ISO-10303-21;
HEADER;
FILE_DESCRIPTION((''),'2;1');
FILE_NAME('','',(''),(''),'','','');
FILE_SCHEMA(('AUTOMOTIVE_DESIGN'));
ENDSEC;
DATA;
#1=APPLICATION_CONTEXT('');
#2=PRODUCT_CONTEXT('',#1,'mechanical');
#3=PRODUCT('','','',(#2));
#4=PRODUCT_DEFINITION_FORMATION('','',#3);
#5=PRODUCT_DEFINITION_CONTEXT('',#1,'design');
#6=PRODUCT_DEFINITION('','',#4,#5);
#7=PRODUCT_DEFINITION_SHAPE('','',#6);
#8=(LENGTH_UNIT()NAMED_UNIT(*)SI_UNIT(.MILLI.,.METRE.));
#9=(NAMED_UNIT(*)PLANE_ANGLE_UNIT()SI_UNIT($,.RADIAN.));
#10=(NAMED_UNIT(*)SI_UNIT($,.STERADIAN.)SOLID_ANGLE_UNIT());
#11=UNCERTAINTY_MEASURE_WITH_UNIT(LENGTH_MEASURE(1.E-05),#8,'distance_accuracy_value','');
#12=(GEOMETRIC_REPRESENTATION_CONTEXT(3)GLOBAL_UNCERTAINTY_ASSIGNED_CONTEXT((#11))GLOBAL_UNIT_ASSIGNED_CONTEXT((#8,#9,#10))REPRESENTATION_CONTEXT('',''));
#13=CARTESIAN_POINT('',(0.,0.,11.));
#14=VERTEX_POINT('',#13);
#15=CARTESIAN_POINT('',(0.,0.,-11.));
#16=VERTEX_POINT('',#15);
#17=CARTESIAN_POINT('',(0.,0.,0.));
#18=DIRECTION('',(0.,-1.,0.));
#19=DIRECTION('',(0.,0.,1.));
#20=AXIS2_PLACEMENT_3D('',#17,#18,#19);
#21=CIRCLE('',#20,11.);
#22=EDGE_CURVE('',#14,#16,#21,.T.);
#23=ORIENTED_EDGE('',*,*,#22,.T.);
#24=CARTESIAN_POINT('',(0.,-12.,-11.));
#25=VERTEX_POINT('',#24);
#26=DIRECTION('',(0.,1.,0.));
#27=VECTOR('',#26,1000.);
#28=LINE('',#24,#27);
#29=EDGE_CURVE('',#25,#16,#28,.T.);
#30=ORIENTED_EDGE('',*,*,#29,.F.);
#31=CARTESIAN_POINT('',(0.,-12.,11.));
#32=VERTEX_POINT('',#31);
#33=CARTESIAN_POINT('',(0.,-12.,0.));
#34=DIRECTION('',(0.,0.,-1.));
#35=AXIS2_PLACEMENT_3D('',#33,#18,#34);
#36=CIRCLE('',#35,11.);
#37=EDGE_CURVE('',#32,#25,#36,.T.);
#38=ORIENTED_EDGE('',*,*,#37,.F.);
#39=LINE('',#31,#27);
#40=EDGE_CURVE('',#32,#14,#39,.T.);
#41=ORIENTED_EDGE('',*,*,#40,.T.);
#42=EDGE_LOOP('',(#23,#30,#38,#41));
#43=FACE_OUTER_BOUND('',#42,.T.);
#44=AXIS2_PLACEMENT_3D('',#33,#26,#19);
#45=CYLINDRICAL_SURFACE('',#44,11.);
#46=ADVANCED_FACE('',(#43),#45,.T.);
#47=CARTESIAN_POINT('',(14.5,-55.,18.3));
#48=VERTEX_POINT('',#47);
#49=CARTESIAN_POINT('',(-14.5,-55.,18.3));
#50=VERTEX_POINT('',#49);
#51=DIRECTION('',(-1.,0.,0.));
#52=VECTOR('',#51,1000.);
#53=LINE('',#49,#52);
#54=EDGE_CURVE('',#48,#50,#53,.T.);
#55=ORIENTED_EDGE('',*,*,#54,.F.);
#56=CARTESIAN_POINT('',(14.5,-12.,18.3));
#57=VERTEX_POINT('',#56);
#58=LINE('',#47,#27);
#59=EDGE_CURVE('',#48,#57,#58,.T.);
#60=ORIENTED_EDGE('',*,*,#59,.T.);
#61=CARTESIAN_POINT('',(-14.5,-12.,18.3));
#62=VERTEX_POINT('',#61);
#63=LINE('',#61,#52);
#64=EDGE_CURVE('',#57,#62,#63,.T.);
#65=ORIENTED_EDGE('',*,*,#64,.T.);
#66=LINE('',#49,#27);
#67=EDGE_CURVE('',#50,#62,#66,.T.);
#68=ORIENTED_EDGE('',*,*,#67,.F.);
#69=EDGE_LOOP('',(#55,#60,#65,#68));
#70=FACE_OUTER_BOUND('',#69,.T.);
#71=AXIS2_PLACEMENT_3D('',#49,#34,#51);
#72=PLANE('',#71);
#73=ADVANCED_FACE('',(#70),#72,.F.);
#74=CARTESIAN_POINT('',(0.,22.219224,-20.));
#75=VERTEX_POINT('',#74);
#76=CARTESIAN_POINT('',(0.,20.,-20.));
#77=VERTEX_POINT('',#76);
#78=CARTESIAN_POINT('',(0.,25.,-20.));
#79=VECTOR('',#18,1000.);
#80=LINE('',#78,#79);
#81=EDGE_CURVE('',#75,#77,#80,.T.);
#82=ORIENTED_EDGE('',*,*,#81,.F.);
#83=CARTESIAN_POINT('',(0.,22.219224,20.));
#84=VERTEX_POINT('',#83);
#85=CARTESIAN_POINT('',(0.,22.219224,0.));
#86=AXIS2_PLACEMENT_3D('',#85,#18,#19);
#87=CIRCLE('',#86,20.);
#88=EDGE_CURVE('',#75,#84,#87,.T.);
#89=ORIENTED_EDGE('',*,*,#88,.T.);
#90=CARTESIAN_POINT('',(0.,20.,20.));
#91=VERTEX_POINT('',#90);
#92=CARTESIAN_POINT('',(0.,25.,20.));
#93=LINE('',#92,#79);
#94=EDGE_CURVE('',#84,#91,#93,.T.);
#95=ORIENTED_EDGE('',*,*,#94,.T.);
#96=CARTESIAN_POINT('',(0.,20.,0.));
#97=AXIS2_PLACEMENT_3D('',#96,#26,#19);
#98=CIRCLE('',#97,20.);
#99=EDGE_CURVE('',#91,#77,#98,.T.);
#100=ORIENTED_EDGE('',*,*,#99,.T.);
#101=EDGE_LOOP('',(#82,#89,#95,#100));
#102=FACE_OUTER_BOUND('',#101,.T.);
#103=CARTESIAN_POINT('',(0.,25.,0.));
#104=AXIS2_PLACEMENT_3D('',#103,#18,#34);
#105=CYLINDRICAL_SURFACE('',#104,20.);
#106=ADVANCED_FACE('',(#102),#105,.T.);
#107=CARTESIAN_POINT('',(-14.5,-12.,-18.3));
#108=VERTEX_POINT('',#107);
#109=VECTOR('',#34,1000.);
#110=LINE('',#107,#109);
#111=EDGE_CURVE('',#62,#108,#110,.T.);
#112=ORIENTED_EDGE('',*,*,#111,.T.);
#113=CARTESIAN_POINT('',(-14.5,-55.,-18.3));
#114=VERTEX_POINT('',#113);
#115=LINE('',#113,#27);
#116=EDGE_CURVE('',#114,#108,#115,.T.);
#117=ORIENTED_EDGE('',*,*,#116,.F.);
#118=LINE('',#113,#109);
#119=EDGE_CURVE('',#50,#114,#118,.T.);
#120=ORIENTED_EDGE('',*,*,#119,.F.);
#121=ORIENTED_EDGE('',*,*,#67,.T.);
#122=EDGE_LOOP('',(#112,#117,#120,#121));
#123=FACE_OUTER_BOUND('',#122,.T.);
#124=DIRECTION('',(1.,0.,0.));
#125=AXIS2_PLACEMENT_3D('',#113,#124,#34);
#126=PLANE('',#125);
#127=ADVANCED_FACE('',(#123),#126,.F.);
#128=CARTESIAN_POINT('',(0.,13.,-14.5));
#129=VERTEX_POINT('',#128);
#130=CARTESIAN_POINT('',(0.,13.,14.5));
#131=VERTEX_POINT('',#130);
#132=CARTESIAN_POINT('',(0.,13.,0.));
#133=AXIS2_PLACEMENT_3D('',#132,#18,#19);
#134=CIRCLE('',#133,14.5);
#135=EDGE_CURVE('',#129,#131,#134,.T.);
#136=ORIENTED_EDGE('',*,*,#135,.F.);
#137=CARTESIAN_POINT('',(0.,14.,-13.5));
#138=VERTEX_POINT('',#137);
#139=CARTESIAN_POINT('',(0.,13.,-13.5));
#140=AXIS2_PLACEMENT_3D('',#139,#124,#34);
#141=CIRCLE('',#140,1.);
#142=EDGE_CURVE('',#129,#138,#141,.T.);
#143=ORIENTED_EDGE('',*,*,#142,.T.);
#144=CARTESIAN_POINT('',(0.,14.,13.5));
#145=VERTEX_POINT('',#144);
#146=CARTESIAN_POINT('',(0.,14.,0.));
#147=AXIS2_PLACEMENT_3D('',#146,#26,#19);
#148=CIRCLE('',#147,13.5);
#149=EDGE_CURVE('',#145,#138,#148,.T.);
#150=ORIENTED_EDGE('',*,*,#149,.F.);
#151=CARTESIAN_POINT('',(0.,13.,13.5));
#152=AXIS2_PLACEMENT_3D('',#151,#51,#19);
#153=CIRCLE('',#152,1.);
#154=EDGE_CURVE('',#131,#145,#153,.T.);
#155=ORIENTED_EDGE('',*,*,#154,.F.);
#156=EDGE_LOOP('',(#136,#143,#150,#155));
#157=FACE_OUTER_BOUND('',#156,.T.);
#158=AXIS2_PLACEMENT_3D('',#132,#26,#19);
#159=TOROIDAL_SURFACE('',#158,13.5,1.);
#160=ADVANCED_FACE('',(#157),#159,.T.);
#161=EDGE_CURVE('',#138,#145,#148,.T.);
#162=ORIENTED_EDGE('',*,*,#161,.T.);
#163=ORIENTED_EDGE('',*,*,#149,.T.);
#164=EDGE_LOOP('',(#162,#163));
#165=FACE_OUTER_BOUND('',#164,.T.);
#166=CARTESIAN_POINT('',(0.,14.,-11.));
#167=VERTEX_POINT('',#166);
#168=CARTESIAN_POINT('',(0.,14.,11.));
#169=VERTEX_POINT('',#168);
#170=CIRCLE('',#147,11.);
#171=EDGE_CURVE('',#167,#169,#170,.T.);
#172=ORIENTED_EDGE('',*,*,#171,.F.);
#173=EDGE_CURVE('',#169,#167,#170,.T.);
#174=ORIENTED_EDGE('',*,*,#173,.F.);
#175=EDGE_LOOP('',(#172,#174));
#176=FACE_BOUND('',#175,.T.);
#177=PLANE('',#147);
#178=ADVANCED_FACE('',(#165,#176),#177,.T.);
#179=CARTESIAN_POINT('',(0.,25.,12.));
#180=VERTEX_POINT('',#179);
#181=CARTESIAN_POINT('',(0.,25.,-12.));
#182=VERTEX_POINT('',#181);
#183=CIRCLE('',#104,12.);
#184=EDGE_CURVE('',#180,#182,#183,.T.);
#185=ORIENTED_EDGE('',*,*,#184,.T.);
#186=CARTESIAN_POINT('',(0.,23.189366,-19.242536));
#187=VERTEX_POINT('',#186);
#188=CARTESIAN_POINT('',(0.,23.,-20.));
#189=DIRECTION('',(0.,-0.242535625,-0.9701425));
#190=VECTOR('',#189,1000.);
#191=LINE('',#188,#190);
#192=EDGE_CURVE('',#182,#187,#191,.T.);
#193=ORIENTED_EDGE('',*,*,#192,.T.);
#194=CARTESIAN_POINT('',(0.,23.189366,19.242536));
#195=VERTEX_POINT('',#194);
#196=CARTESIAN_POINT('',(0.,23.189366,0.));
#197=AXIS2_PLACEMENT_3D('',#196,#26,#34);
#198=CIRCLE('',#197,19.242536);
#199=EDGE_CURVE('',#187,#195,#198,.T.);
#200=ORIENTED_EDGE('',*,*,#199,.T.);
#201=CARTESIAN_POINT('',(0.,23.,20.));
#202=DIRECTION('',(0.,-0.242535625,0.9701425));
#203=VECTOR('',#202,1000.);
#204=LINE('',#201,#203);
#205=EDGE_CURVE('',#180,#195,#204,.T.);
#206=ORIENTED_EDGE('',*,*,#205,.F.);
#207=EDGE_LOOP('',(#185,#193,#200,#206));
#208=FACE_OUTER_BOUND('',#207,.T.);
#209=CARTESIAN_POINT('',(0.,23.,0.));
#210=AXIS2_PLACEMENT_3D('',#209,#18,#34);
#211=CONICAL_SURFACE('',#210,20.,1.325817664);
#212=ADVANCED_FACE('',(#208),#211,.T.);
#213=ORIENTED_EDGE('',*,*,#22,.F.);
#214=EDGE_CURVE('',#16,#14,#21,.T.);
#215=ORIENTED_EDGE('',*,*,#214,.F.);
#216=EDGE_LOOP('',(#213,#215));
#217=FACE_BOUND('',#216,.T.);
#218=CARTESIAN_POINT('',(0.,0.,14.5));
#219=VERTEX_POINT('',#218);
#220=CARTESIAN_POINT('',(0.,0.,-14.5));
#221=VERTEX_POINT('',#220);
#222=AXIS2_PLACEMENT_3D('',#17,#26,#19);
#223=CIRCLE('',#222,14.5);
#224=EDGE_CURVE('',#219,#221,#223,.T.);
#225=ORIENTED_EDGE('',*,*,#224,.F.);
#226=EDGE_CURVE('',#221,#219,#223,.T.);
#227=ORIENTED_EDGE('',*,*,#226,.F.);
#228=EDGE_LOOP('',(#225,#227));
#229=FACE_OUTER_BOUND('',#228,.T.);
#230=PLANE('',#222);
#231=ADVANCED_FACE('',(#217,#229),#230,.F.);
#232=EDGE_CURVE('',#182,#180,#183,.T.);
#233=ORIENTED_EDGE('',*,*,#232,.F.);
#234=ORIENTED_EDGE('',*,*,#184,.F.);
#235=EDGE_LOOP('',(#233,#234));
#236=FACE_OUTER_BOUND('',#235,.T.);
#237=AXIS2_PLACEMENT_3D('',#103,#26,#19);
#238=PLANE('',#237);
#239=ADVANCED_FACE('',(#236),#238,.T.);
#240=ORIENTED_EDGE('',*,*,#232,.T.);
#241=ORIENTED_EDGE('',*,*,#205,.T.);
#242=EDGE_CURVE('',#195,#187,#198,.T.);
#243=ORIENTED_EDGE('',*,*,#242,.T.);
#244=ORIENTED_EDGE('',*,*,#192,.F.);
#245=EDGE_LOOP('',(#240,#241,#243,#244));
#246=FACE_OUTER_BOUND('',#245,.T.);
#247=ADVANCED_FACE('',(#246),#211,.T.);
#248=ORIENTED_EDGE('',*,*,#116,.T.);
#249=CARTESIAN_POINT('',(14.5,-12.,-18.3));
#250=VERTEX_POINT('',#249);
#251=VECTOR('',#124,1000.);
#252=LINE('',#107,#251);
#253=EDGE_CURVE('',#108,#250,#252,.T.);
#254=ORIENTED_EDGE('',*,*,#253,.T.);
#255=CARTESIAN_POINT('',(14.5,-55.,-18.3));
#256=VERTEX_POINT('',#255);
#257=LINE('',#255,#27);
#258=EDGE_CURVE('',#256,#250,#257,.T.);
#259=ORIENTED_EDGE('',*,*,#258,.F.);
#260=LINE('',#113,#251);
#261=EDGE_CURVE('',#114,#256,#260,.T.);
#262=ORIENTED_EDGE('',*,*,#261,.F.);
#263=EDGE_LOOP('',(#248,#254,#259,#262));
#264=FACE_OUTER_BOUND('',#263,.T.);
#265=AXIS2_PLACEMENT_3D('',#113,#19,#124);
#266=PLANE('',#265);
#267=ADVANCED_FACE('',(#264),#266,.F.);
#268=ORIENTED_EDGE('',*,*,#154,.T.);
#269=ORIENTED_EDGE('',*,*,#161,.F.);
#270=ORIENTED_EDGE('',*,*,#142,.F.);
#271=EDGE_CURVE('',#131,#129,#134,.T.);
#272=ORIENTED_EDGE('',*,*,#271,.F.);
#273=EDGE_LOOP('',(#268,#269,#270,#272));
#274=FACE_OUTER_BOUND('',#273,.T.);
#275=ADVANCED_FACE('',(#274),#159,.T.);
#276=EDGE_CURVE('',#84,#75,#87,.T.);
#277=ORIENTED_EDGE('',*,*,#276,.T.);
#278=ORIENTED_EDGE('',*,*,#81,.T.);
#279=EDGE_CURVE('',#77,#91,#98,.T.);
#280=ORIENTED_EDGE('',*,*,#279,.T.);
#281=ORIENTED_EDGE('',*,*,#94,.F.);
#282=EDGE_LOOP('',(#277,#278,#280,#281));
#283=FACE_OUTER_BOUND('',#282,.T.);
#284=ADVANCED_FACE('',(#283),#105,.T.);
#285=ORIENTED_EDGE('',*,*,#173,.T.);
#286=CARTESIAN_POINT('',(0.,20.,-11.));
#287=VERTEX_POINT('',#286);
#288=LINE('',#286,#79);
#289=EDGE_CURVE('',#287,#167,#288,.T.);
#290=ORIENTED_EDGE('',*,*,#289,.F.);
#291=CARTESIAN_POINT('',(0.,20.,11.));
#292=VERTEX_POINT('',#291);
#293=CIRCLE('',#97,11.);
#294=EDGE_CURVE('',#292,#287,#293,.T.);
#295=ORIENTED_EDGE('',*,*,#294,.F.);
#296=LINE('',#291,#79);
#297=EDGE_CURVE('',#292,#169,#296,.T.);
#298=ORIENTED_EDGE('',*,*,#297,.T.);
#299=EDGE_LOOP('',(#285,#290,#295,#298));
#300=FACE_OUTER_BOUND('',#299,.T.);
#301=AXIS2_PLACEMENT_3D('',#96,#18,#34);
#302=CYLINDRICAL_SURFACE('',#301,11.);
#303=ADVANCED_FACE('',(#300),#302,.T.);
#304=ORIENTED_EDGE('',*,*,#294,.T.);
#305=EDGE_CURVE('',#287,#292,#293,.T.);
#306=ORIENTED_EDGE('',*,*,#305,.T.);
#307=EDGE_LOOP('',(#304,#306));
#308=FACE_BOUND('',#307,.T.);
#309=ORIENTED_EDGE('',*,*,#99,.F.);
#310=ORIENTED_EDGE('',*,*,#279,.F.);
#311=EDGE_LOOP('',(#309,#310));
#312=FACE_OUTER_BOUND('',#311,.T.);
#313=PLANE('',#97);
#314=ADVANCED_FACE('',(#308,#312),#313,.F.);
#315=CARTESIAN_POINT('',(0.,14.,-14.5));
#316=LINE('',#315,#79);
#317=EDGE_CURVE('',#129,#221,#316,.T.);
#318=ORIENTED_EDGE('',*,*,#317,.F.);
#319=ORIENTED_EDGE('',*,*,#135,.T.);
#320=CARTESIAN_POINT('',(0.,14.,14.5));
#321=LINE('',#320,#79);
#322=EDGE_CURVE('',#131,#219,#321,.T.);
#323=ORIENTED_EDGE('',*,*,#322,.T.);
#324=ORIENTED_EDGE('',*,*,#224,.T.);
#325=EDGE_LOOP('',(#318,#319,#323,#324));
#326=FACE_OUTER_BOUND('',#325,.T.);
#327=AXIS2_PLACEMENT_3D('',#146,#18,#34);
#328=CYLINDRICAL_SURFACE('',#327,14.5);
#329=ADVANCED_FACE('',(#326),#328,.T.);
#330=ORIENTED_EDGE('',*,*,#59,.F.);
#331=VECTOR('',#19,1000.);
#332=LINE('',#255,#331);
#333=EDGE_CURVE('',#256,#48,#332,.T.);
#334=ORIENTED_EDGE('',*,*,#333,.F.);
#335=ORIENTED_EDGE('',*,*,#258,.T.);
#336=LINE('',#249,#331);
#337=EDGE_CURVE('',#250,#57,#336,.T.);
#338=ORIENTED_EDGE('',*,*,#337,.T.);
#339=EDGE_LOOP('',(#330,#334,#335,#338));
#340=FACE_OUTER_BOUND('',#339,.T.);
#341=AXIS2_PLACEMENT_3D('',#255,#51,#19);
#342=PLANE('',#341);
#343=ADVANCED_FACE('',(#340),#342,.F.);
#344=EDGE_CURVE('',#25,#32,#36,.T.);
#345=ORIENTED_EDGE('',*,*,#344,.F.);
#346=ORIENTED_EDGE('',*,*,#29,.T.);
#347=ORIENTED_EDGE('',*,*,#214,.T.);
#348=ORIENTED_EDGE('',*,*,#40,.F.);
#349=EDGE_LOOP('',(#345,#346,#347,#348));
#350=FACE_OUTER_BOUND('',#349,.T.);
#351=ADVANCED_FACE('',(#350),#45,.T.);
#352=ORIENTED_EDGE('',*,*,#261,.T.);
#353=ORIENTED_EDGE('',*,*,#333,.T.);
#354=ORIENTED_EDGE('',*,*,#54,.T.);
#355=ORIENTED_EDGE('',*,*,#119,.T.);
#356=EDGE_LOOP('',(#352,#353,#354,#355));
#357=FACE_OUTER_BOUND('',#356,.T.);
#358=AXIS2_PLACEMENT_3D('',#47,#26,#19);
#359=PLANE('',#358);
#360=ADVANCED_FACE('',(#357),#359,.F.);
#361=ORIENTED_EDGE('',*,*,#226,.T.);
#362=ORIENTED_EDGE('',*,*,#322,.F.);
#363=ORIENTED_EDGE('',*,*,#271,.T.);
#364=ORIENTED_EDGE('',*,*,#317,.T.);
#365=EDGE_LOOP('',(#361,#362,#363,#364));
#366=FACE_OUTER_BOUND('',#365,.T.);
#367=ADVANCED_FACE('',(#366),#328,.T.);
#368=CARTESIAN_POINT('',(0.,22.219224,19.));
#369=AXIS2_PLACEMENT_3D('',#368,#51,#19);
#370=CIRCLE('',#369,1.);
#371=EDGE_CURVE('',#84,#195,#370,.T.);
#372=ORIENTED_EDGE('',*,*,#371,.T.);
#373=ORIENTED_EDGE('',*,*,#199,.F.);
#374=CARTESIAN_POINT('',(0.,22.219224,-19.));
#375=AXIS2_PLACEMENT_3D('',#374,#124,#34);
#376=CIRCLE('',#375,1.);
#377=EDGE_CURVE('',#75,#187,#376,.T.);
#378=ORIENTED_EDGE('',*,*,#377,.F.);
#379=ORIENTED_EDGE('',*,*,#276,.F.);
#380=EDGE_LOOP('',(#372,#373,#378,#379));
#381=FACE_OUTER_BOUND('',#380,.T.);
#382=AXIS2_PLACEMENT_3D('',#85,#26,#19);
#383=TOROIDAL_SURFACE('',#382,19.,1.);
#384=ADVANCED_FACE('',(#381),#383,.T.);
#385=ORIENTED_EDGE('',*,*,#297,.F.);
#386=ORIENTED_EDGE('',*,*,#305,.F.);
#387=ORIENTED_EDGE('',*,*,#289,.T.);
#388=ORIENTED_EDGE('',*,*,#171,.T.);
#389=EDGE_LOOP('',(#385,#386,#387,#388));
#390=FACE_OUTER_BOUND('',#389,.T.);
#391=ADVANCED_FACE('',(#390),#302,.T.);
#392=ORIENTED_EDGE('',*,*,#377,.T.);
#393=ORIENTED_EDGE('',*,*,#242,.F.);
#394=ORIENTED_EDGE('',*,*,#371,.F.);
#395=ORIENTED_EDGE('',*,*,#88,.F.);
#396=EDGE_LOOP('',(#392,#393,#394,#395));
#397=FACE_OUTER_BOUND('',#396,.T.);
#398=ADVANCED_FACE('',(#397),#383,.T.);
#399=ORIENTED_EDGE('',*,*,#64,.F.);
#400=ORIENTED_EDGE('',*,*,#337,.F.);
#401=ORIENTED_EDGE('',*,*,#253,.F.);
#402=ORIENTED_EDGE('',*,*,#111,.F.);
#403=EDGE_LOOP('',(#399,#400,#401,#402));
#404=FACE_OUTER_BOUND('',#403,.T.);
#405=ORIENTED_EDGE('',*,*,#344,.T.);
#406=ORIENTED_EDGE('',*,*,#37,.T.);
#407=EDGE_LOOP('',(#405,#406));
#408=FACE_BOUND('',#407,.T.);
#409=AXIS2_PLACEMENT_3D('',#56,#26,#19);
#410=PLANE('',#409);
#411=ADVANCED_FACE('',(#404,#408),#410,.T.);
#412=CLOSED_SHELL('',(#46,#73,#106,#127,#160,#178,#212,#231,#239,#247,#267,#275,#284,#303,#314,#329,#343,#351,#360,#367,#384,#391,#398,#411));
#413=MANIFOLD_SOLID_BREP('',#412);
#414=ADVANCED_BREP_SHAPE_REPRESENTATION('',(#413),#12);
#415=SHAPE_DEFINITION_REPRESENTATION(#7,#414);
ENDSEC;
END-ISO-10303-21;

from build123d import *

# Parameters (mm, degrees)
SKETCH1_R           = 14.5
BOSS_EXTRUDE1_DEPTH = 14
SKETCH2_R           = 11
BOSS_EXTRUDE2_DEPTH = 6
SKETCH3_R           = 20
BOSS_EXTRUDE3_DEPTH = 5
FILLET1_R           = 1
BOSS_EXTRUDE4_START = 12
SKETCH5_R           = 11
BOSS_EXTRUDE4_DEPTH = 12
SKETCH6_W           = 29
SKETCH6_H           = 36.6
BOSS_EXTRUDE5_DEPTH = 43


with BuildPart() as part:
    # Sketch1 → Boss-Extrude1 (new body)
    with BuildSketch(Plane(origin=(0, 0, 0), x_dir=(1, 0, 0), z_dir=(0, 1, 0))):
        with Locations(Location((0, 0, 0), (0, 0, 270))):
            Circle(SKETCH1_R)
    extrude(amount=BOSS_EXTRUDE1_DEPTH)

    # Sketch2 → Boss-Extrude2 (add)
    with BuildSketch(Plane(origin=(0, 14, 0), x_dir=(1, 0, 0), z_dir=(0, 1, 0))):
        with Locations(Location((0, 0, 0), (0, 0, 270))):
            Circle(SKETCH2_R)
    extrude(amount=BOSS_EXTRUDE2_DEPTH)

    # Sketch3 → Boss-Extrude3 (add)
    with BuildSketch(Plane(origin=(0, 20, 0), x_dir=(1, 0, 0), z_dir=(0, 1, 0))):
        with Locations(Location((0, 0, 0), (0, 0, 270))):
            Circle(SKETCH3_R)
    extrude(amount=BOSS_EXTRUDE3_DEPTH)

    # Sketch4 → Cut-Revolve1 (revolve, cut)
    with BuildSketch(Plane.XY, mode=Mode.PRIVATE) as cut_revolve1_sk:
        Polygon((-12, 25), (-20, 25), (-20, 23), align=None)
    revolve(cut_revolve1_sk.sketch.rotate(Axis((0, 0, 0), (0, 1, 0)), 270), axis=Axis((0, 0, 0), (0, 1, 0)), mode=Mode.SUBTRACT)

    # Fillet1
    fillet1_edges = [part.edges().sort_by_distance(p)[0] for p in [
        (-20, 23, 0),
        (0, 14, -14.5),
    ]]
    fillet(fillet1_edges, radius=FILLET1_R)

    # Sketch5 → Boss-Extrude4 (add)
    with BuildSketch(Plane.XZ.offset(BOSS_EXTRUDE4_START)):
        with Locations(Location((0, 0, 0), (0, 0, 90))):
            Circle(SKETCH5_R)
    extrude(amount=-BOSS_EXTRUDE4_DEPTH)

    # Sketch6 → Boss-Extrude5 (add)
    with BuildSketch(Plane.XZ.offset(12)):
        Rectangle(SKETCH6_W, SKETCH6_H)
    extrude(amount=BOSS_EXTRUDE5_DEPTH)


solid = part.part
